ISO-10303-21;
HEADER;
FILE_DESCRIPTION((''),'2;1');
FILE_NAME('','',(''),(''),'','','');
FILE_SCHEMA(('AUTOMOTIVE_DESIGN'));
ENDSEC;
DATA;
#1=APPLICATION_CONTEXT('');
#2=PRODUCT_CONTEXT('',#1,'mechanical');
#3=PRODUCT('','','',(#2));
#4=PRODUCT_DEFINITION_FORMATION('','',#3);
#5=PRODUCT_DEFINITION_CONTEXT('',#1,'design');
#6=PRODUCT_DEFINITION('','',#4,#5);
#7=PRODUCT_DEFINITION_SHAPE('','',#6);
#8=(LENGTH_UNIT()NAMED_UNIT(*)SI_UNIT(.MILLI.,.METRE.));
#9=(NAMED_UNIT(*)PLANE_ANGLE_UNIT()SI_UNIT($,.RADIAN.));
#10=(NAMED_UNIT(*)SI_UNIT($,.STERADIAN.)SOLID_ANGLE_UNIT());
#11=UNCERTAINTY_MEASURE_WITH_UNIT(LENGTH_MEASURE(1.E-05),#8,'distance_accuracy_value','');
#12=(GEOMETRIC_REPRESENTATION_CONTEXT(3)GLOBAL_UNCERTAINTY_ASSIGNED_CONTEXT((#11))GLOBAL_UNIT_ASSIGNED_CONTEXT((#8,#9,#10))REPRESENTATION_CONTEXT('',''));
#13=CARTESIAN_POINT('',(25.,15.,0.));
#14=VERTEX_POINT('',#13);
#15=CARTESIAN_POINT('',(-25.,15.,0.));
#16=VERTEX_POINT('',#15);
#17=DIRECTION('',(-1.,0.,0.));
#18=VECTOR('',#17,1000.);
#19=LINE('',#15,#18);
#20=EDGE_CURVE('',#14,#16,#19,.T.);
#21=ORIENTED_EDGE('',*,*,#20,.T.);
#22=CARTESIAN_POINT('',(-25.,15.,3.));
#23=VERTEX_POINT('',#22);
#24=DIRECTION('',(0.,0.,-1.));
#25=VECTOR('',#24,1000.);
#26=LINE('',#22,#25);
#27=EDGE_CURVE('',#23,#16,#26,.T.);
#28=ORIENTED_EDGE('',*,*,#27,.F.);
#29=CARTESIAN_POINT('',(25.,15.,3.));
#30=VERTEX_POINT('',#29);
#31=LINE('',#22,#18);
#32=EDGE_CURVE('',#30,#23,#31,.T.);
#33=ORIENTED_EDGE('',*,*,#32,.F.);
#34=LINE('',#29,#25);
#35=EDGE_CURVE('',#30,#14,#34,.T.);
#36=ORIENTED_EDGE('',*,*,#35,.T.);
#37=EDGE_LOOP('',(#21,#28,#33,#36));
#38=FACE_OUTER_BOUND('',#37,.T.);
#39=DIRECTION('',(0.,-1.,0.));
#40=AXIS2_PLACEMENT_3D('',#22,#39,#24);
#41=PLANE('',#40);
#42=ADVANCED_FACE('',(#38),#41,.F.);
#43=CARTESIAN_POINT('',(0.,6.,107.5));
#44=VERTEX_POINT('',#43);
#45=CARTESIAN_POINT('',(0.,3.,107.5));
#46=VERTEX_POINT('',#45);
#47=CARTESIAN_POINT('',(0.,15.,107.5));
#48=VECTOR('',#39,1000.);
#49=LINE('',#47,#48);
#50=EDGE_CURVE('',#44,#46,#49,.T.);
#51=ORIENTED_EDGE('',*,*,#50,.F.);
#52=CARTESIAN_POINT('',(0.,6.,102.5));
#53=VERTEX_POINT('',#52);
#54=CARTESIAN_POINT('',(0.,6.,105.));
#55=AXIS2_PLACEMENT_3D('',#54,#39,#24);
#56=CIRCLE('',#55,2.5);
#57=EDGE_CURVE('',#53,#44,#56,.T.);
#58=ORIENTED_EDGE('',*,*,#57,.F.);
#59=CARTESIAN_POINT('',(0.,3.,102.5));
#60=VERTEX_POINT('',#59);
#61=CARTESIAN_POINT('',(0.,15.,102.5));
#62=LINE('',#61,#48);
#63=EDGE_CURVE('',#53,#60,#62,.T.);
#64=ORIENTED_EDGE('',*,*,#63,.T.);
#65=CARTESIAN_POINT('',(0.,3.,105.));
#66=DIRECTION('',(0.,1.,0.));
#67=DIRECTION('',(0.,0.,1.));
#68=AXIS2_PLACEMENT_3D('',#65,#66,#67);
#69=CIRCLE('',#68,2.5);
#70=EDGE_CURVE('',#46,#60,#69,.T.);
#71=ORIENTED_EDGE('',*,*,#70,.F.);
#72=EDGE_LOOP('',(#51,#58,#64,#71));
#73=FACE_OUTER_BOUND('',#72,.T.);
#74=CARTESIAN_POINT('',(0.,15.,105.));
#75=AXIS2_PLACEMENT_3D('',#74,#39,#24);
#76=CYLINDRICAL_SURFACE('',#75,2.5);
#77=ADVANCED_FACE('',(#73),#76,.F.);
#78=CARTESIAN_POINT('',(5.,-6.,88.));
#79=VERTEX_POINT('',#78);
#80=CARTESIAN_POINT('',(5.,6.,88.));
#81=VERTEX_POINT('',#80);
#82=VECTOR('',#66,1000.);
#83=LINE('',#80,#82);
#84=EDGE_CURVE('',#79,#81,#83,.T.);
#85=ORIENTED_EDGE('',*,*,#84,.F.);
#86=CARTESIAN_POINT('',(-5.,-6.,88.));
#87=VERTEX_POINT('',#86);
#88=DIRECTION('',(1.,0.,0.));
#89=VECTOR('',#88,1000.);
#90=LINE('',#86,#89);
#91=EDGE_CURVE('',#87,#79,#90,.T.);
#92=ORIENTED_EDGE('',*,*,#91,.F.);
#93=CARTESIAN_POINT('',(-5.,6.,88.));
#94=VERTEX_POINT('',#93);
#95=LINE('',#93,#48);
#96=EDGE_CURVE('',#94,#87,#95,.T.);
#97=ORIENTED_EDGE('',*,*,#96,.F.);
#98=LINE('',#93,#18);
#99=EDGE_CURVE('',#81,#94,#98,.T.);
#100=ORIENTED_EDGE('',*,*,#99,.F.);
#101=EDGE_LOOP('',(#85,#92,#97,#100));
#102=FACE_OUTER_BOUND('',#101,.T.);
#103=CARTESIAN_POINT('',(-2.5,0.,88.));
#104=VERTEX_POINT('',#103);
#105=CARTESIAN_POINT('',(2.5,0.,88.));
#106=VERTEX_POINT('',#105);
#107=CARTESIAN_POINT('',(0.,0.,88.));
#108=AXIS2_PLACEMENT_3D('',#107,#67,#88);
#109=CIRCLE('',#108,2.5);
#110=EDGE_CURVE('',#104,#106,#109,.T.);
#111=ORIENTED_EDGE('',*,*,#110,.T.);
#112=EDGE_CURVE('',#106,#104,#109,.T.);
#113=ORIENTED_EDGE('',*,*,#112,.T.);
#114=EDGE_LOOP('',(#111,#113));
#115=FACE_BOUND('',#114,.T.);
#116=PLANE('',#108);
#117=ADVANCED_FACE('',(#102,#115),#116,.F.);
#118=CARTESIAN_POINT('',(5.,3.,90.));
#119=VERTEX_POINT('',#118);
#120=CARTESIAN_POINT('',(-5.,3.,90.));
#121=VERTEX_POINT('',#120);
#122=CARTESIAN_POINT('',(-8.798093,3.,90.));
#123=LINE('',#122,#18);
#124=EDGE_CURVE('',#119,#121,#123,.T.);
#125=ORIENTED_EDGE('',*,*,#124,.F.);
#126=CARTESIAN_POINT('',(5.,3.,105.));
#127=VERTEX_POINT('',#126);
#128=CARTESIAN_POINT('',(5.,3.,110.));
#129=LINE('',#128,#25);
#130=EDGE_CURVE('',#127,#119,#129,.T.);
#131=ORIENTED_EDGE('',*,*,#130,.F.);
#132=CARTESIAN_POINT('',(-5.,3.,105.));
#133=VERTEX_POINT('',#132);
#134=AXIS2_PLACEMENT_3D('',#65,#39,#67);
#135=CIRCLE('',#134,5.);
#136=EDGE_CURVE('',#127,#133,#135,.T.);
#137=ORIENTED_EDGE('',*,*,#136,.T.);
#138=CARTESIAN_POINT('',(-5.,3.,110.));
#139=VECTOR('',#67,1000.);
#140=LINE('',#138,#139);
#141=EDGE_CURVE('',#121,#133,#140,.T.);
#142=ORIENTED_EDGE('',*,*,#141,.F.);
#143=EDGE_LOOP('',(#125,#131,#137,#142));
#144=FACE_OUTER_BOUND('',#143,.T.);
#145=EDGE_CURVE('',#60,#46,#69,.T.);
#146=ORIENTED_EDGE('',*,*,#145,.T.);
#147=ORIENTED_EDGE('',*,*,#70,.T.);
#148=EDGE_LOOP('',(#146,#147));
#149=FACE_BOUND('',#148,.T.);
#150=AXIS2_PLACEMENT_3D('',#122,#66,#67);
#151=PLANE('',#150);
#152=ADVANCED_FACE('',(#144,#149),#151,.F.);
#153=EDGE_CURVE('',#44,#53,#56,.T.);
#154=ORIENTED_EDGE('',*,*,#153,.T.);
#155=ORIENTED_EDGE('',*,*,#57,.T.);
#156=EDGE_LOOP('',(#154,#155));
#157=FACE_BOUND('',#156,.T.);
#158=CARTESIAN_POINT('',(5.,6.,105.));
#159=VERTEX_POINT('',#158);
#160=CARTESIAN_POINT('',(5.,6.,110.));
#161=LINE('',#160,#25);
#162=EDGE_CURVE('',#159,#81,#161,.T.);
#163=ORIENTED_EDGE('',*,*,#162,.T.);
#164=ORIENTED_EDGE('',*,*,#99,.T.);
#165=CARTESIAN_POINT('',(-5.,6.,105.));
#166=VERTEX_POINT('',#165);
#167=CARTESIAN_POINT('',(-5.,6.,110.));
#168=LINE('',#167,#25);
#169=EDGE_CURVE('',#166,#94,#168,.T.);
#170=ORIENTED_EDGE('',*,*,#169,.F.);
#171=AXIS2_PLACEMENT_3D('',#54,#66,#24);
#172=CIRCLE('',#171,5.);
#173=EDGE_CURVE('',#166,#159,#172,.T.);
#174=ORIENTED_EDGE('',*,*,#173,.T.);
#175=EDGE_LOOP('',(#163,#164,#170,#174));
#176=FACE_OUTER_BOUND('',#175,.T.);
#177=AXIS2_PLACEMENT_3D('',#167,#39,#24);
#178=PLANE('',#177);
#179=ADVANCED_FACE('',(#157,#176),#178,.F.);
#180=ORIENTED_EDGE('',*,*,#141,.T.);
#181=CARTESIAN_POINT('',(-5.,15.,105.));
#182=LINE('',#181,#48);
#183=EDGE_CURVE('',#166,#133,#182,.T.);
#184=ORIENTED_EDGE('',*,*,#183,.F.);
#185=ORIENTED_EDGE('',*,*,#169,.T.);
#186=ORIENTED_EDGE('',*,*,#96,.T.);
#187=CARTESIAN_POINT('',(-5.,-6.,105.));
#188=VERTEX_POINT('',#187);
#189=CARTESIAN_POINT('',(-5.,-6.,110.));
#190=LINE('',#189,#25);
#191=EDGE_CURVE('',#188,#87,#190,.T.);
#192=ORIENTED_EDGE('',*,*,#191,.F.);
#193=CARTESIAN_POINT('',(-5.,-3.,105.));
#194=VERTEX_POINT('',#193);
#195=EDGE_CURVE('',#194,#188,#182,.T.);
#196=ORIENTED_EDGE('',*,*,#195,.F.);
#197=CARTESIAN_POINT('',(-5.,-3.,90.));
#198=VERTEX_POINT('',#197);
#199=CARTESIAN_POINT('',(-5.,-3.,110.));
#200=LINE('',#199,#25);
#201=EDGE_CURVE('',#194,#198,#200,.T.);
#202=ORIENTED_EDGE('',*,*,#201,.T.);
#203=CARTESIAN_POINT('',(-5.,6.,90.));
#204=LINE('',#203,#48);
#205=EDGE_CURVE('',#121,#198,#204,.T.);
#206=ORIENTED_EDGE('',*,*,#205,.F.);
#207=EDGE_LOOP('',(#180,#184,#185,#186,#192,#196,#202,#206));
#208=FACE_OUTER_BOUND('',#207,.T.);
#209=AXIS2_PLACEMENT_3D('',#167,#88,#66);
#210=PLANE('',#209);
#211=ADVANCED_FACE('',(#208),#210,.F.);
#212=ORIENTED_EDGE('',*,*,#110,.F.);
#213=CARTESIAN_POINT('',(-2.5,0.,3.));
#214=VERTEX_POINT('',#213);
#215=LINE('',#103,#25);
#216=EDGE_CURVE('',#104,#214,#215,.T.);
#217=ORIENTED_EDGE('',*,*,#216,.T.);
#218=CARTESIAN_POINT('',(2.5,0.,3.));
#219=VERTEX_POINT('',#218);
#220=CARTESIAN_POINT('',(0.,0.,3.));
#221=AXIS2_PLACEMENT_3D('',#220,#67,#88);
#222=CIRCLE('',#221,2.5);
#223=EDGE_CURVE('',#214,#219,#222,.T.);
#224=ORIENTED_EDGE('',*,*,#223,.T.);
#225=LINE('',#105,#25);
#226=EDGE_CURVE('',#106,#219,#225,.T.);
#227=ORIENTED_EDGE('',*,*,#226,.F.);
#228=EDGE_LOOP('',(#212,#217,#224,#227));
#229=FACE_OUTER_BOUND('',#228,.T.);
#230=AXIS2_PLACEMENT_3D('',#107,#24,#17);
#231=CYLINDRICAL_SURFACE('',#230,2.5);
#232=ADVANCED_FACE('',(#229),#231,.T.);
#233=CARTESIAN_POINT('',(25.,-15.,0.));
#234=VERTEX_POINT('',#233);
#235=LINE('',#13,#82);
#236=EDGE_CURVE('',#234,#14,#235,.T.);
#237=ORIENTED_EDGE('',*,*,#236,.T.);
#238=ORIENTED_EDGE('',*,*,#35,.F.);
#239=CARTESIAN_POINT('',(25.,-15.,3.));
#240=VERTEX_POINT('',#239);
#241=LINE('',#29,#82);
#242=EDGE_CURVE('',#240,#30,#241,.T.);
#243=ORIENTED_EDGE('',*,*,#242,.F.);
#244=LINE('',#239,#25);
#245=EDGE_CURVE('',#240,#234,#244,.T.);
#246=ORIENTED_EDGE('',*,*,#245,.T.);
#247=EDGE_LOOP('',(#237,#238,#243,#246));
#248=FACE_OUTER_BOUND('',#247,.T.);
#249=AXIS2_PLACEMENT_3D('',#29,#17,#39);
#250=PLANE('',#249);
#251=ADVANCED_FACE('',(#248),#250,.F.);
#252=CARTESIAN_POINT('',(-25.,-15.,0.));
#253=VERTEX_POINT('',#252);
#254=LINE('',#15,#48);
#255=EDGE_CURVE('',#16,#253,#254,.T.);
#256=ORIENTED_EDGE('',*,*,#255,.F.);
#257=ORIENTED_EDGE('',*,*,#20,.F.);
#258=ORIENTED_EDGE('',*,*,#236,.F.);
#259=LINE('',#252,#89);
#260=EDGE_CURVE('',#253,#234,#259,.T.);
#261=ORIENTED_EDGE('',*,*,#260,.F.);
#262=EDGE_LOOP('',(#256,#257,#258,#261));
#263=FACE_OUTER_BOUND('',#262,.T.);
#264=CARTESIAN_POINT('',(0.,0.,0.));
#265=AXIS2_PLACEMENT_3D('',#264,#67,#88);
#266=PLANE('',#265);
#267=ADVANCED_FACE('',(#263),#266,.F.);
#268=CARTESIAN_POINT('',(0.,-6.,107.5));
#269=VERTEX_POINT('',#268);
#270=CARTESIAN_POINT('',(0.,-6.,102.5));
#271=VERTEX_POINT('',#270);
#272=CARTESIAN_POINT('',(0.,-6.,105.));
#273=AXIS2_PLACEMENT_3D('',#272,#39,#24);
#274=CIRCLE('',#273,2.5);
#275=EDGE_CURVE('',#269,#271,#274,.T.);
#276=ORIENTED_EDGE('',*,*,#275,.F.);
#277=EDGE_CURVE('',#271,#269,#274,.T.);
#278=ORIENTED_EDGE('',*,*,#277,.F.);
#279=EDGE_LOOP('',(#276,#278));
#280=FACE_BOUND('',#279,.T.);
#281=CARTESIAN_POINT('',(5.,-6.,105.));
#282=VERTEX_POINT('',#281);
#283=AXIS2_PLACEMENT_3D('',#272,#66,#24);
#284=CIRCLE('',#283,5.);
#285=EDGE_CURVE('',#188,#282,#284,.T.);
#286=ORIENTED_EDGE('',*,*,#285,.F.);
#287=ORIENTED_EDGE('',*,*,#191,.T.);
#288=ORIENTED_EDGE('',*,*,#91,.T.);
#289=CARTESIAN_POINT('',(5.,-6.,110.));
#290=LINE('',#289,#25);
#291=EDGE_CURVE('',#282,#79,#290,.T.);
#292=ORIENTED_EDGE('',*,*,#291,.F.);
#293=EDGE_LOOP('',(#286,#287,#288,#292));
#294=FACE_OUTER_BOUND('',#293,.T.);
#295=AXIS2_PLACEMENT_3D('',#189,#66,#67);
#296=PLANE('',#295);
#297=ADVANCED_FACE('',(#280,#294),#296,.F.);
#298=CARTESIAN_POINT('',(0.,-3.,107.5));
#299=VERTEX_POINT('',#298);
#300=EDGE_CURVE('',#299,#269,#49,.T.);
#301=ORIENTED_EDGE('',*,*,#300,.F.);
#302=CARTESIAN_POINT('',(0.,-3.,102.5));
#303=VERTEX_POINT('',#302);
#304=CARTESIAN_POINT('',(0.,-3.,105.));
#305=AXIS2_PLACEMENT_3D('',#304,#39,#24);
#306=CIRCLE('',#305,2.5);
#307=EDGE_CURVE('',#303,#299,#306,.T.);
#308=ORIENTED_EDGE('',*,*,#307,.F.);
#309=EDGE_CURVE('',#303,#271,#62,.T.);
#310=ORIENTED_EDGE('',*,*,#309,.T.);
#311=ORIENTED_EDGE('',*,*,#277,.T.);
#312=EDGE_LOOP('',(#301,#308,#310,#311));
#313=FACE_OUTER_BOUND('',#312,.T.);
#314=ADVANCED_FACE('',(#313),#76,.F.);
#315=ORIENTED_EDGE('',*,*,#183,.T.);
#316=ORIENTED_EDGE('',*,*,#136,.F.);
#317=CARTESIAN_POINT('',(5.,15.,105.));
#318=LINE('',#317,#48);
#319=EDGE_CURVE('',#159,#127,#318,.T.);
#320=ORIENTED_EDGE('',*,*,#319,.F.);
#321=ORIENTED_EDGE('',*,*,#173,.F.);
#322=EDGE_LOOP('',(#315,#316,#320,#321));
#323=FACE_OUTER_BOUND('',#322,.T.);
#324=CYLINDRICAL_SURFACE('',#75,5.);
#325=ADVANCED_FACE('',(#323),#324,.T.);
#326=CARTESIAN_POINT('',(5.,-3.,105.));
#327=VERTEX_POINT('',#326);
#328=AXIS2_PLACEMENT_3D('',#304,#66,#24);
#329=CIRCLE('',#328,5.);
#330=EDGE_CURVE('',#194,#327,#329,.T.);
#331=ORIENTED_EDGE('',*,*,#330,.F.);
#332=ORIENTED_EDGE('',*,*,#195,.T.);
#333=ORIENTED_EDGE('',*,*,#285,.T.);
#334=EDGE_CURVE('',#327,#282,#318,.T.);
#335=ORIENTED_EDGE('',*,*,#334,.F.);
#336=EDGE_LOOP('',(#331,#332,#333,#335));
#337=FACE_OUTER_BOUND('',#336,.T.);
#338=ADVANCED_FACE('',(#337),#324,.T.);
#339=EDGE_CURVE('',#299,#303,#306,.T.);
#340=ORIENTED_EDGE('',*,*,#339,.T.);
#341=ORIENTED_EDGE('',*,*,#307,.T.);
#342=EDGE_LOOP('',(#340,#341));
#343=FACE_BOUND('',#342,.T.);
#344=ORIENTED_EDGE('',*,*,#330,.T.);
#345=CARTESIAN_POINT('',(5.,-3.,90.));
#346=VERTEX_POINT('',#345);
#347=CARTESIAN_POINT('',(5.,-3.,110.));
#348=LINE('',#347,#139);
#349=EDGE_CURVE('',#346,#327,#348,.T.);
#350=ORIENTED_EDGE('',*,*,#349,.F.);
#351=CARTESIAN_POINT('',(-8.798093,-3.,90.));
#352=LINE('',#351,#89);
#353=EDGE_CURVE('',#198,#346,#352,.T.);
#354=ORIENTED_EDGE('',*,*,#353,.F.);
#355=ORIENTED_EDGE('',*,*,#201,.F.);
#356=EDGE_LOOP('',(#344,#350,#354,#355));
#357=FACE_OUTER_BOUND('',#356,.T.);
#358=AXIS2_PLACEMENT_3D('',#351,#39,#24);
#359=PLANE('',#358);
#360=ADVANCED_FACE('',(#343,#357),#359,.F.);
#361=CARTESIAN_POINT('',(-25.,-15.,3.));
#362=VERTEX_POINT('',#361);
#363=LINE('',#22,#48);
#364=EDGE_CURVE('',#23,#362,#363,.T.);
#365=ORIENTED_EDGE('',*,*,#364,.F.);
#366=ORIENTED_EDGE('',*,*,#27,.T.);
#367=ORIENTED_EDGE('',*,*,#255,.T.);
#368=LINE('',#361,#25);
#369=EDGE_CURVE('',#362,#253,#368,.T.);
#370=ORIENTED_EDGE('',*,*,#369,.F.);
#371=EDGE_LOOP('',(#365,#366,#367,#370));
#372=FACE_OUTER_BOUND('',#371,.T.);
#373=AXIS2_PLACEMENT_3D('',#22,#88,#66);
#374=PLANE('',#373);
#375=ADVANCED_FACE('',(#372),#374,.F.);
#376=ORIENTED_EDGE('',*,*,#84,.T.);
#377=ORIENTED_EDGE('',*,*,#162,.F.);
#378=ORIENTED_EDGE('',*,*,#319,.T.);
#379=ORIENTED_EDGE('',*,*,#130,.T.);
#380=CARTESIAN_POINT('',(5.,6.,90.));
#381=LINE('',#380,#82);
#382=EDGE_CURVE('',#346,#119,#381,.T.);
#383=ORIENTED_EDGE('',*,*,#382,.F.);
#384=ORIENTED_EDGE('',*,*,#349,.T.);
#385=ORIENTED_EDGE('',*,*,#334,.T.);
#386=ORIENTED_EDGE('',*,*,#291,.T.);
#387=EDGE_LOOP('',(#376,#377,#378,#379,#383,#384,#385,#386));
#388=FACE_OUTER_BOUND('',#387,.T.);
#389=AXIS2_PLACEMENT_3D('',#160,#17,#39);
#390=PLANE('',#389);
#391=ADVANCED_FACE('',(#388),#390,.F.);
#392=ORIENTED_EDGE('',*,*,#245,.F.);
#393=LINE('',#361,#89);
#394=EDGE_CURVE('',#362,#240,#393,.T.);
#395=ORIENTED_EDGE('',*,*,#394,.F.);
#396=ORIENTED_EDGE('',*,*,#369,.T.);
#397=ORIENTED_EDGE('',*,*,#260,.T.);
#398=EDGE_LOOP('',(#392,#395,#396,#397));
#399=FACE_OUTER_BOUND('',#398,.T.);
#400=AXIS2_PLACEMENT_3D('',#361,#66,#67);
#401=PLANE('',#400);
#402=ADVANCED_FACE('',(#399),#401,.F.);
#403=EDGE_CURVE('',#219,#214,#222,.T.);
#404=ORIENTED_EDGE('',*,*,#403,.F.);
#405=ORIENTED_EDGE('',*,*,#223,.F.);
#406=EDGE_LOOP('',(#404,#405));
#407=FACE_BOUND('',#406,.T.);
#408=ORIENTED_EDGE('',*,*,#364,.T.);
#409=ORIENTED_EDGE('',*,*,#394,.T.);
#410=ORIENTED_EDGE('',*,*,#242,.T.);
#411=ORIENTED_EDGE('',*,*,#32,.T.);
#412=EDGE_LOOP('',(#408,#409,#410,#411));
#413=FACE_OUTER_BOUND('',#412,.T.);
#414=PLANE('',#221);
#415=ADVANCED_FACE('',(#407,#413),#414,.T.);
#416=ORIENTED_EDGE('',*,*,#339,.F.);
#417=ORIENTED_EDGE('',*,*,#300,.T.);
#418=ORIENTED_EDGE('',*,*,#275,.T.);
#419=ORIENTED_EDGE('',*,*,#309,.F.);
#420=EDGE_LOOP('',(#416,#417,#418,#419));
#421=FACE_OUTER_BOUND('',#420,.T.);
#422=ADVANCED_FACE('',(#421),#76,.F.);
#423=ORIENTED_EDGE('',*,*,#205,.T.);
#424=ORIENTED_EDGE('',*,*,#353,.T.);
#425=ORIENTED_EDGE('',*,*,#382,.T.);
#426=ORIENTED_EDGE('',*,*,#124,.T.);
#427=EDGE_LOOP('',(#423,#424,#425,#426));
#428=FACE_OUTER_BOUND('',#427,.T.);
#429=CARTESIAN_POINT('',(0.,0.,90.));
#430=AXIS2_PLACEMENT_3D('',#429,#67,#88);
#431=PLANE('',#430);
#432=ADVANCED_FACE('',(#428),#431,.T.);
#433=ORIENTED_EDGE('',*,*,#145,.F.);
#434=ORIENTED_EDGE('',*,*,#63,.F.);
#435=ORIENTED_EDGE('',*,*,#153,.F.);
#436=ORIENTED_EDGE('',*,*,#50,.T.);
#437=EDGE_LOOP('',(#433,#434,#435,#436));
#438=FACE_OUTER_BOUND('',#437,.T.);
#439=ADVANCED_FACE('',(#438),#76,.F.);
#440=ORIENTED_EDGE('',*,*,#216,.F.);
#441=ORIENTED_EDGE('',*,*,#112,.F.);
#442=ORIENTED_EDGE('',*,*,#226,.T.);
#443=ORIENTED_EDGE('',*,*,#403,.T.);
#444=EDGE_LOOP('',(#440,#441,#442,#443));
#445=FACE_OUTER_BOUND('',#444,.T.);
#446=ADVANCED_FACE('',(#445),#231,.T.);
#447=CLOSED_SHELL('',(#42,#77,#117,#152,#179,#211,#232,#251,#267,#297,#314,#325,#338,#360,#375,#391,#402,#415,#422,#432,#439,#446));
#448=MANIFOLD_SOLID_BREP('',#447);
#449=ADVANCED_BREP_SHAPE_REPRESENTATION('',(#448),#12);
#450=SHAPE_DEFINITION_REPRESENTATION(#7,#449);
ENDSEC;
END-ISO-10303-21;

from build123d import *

# Parameters (mm, degrees)
SKETCH1_W           = 50
SKETCH1_H           = 30
BOSS_EXTRUDE1_DEPTH = 3
SKETCH2_R           = 2.5
BOSS_EXTRUDE2_DEPTH = 85
SKETCH3_W           = 10
SKETCH3_H           = 12
BOSS_EXTRUDE3_DEPTH = 22
SKETCH4_W           = 17.596186584
SKETCH4_H           = 6
CUT_EXTRUDE1_DEPTH  = 20
SKETCH5_R           = 2.5
CUT_EXTRUDE2_DEPTH  = 115.743191519


with BuildPart() as part:
    # Sketch1 → Boss-Extrude1 (new body)
    with BuildSketch(Plane.XY):
        Rectangle(SKETCH1_W, SKETCH1_H)
    extrude(amount=BOSS_EXTRUDE1_DEPTH)

    # Sketch2 → Boss-Extrude2 (add)
    with BuildSketch(Plane.XY.offset(3)):
        Circle(SKETCH2_R)
    extrude(amount=BOSS_EXTRUDE2_DEPTH)

    # Sketch3 → Boss-Extrude3 (add)
    with BuildSketch(Plane.XY.offset(88)):
        Rectangle(SKETCH3_W, SKETCH3_H)
    extrude(amount=BOSS_EXTRUDE3_DEPTH)

    # Sketch4 → Cut-Extrude1 (cut)
    with BuildSketch(Plane.XY.offset(110)):
        Rectangle(SKETCH4_W, SKETCH4_H)
    extrude(amount=-CUT_EXTRUDE1_DEPTH, mode=Mode.SUBTRACT)

    # Sketch5 → Cut-Extrude2 (cut, through all)
    with BuildSketch(Plane(origin=(0, -6, 0), x_dir=(-1, 0, 0), z_dir=(0, -1, 0))):
        with Locations(Location((0, -105, 0), (0, 0, 90))):
            Circle(SKETCH5_R)
        with BuildLine():
            Line((5, -105), (16.865416132, -140.325641039))
            Line((16.865416132, -140.325641039), (-16.120021854, -140.325641039))
            Line((-16.120021854, -140.325641039), (-5, -105))
            ThreePointArc((-5, -105), (0, -110), (5, -105))
        make_face()
    extrude(amount=-CUT_EXTRUDE2_DEPTH, mode=Mode.SUBTRACT)


solid = part.part
